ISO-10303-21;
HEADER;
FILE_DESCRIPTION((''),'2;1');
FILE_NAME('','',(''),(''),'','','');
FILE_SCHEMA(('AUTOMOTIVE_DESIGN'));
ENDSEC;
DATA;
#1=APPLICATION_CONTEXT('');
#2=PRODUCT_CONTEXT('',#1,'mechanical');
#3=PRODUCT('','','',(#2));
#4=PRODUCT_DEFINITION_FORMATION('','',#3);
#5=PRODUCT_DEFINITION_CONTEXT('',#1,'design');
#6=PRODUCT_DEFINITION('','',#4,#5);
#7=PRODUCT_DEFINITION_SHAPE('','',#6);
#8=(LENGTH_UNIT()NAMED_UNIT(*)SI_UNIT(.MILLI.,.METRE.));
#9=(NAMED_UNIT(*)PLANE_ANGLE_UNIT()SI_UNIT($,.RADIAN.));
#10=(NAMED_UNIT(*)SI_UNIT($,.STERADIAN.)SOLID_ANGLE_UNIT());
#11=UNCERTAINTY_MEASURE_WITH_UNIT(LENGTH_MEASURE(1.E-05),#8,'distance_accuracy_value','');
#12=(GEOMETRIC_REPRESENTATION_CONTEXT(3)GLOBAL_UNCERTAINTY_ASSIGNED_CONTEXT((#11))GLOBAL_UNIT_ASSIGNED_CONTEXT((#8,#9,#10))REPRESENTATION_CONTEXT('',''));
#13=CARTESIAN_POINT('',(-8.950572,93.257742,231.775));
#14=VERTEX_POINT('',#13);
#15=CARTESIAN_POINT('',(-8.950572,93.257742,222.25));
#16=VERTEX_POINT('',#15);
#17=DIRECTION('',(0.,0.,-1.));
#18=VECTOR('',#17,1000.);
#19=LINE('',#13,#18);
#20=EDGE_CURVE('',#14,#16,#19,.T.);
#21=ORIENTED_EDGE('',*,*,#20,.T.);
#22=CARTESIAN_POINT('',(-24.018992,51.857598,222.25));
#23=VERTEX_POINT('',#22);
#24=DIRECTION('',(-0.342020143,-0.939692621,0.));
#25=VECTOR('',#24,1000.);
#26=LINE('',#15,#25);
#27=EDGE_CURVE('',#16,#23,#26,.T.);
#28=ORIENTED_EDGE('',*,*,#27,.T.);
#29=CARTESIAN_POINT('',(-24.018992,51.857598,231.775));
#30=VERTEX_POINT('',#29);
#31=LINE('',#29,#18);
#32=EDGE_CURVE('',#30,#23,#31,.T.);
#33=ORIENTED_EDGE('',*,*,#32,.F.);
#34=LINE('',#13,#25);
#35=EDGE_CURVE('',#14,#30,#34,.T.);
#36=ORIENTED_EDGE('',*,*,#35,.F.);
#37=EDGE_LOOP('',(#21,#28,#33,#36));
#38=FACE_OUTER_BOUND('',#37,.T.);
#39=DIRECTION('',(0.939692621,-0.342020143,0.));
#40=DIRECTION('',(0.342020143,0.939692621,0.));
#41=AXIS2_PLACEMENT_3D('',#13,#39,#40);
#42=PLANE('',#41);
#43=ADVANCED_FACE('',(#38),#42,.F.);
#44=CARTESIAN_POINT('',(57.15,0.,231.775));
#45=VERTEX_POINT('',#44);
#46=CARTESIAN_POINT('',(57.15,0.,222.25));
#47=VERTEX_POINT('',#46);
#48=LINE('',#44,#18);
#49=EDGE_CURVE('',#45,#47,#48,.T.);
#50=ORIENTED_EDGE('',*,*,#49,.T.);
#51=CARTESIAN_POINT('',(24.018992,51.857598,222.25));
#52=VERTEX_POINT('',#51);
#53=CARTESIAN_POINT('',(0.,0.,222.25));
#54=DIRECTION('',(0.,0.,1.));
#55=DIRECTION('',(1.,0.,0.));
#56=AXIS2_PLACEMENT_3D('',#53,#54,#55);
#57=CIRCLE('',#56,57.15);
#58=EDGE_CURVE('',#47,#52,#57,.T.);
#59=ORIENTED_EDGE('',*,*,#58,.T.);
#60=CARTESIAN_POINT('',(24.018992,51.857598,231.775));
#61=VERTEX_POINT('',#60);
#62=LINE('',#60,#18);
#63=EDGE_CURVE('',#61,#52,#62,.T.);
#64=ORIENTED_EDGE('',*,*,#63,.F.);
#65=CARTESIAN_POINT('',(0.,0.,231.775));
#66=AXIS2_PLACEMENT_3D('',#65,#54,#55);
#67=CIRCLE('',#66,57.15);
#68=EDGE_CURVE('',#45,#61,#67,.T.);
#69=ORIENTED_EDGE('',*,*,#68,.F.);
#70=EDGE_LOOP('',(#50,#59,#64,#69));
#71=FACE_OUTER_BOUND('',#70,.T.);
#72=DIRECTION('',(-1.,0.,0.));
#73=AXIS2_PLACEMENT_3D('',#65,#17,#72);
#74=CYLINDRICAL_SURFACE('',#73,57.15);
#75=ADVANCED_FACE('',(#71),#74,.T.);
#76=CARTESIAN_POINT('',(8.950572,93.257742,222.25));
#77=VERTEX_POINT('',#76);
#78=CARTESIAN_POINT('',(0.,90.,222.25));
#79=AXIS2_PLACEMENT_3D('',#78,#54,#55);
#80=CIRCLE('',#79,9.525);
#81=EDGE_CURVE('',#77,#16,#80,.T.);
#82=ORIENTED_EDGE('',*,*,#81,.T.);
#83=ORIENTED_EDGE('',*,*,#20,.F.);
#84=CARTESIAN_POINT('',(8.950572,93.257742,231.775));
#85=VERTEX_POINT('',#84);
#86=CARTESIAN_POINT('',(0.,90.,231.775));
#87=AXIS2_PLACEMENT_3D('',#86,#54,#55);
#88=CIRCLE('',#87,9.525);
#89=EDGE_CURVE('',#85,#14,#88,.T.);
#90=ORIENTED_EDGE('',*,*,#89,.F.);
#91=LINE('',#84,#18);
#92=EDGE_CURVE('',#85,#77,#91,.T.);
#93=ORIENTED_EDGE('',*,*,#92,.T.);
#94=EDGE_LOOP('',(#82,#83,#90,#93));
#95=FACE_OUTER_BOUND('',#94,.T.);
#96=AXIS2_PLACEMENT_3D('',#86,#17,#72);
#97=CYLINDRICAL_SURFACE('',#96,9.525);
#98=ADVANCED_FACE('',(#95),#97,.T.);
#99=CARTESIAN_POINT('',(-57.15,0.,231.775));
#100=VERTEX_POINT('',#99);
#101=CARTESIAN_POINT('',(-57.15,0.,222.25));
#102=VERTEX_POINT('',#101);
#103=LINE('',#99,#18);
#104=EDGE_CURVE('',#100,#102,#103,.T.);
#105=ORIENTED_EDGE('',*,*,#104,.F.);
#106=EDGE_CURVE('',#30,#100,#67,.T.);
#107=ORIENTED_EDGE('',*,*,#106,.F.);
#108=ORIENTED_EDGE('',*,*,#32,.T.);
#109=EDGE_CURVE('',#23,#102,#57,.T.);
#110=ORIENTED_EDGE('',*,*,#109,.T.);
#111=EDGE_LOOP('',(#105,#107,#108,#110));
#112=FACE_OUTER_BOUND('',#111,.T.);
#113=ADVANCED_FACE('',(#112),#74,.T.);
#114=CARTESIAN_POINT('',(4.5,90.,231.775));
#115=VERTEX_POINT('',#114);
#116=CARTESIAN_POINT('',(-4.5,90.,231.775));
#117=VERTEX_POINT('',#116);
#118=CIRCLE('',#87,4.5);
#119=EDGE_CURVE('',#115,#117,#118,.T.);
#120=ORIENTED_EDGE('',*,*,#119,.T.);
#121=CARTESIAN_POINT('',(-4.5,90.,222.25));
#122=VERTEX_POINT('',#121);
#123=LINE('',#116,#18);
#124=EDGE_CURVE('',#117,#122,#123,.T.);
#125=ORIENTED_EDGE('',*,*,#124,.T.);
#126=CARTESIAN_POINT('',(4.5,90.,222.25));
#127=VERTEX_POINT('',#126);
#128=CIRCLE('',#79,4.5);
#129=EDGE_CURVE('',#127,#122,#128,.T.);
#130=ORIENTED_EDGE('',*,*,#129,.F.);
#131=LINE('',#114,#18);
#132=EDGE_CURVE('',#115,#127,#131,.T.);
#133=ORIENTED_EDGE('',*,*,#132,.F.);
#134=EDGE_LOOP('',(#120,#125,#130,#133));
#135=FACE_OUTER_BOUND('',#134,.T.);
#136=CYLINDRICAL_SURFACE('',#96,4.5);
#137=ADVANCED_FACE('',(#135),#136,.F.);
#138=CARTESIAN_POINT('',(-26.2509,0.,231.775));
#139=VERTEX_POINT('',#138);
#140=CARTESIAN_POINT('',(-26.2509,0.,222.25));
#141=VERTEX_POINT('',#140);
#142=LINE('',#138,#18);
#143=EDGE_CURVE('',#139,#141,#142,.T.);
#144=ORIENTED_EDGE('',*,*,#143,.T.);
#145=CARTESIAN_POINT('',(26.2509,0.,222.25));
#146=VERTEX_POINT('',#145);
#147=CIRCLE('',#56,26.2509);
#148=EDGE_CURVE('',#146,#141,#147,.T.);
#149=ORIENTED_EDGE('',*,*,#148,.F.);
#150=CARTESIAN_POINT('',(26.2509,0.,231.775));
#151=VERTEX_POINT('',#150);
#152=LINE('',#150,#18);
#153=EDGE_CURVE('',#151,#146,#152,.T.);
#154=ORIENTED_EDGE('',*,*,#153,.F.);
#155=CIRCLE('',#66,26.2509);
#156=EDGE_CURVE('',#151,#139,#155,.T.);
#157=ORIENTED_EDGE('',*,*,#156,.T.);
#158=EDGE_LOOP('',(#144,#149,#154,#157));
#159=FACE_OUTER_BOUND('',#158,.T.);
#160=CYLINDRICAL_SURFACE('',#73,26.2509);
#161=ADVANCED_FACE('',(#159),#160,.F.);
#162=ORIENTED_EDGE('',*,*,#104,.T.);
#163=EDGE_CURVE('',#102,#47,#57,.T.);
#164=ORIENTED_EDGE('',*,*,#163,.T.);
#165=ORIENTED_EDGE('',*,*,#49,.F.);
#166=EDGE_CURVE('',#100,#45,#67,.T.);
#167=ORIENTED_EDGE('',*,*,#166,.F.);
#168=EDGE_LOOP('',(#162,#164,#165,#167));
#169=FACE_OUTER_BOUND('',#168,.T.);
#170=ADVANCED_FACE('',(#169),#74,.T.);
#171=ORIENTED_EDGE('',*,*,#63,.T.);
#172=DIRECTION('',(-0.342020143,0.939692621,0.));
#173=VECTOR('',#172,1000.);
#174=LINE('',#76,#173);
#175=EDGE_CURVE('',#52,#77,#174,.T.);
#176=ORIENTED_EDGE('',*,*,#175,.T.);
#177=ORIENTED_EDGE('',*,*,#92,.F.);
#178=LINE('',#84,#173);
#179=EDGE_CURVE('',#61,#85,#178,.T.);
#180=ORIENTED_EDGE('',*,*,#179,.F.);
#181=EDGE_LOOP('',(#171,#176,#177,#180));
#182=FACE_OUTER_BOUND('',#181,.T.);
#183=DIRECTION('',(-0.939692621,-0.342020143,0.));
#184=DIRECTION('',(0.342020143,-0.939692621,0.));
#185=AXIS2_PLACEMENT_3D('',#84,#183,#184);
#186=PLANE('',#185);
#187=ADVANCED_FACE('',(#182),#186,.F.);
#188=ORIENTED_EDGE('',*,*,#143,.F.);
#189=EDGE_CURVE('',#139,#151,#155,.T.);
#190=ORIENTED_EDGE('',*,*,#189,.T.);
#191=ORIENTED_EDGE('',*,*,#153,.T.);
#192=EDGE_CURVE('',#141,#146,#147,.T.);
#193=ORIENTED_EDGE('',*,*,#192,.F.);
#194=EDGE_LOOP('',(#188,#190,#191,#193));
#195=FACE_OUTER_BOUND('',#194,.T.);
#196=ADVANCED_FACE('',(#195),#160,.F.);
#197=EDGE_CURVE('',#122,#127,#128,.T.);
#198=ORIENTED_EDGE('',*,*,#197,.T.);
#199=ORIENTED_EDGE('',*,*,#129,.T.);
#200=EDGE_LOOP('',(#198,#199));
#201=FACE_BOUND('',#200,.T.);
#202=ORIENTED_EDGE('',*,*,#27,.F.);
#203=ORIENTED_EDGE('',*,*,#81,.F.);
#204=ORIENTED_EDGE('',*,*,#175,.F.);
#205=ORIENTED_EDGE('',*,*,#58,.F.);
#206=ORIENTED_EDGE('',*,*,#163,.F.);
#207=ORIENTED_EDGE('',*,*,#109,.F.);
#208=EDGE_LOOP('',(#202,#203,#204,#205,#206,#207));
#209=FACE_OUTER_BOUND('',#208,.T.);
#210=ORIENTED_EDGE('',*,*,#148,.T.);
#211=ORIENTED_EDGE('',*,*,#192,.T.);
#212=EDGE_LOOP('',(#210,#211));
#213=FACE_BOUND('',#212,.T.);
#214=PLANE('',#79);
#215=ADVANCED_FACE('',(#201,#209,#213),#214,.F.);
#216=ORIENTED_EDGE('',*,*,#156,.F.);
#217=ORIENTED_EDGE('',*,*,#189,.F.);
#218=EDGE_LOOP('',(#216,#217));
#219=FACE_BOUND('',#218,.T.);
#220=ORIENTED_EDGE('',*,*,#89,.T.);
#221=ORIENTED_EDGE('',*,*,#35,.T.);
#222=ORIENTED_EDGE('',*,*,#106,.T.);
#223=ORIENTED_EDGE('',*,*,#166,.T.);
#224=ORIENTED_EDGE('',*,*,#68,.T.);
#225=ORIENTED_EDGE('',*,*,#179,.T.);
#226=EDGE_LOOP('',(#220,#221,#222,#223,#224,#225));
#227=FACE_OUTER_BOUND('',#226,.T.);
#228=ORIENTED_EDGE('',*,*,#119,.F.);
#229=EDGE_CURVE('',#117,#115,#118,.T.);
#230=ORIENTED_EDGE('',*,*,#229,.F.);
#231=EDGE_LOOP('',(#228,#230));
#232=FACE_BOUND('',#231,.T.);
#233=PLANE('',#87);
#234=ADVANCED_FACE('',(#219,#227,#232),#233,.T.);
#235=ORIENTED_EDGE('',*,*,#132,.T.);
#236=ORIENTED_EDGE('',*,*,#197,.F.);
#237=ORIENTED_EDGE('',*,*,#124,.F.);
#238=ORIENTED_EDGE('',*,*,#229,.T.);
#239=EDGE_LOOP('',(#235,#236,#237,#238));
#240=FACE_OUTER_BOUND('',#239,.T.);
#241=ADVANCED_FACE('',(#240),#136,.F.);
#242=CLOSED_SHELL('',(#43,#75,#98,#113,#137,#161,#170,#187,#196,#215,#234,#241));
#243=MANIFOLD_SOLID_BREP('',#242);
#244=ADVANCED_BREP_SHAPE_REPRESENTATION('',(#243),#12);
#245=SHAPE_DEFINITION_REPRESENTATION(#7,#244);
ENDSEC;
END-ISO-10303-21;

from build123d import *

# Parameters (mm, degrees)
SKETCH1_R           = 26.2509
SKETCH1_R_2         = 4.5
BOSS_EXTRUDE1_DEPTH = 9.525


with BuildPart() as part:
    # Sketch1 → Boss-Extrude1 (new body)
    with BuildSketch(Plane.XY.offset(222.25)):
        with BuildLine():
            Line((-8.950572213, 93.257741865), (-24.018992106, 51.857598462))
            ThreePointArc((-24.018992106, 51.857598462), (0, -57.15), (24.018992106, 51.857598462))
            Line((24.018992106, 51.857598462), (8.950572213, 93.257741865))
            ThreePointArc((8.950572213, 93.257741865), (0, 99.525), (-8.950572213, 93.257741865))
        make_face()
        with Locations(Location((0, 0, 0), (0, 0, 180))):
            Circle(SKETCH1_R, mode=Mode.SUBTRACT)
        with Locations(Location((0, 90, 0), (0, 0, 180))):
            Circle(SKETCH1_R_2, mode=Mode.SUBTRACT)
    extrude(amount=BOSS_EXTRUDE1_DEPTH)


solid = part.part
